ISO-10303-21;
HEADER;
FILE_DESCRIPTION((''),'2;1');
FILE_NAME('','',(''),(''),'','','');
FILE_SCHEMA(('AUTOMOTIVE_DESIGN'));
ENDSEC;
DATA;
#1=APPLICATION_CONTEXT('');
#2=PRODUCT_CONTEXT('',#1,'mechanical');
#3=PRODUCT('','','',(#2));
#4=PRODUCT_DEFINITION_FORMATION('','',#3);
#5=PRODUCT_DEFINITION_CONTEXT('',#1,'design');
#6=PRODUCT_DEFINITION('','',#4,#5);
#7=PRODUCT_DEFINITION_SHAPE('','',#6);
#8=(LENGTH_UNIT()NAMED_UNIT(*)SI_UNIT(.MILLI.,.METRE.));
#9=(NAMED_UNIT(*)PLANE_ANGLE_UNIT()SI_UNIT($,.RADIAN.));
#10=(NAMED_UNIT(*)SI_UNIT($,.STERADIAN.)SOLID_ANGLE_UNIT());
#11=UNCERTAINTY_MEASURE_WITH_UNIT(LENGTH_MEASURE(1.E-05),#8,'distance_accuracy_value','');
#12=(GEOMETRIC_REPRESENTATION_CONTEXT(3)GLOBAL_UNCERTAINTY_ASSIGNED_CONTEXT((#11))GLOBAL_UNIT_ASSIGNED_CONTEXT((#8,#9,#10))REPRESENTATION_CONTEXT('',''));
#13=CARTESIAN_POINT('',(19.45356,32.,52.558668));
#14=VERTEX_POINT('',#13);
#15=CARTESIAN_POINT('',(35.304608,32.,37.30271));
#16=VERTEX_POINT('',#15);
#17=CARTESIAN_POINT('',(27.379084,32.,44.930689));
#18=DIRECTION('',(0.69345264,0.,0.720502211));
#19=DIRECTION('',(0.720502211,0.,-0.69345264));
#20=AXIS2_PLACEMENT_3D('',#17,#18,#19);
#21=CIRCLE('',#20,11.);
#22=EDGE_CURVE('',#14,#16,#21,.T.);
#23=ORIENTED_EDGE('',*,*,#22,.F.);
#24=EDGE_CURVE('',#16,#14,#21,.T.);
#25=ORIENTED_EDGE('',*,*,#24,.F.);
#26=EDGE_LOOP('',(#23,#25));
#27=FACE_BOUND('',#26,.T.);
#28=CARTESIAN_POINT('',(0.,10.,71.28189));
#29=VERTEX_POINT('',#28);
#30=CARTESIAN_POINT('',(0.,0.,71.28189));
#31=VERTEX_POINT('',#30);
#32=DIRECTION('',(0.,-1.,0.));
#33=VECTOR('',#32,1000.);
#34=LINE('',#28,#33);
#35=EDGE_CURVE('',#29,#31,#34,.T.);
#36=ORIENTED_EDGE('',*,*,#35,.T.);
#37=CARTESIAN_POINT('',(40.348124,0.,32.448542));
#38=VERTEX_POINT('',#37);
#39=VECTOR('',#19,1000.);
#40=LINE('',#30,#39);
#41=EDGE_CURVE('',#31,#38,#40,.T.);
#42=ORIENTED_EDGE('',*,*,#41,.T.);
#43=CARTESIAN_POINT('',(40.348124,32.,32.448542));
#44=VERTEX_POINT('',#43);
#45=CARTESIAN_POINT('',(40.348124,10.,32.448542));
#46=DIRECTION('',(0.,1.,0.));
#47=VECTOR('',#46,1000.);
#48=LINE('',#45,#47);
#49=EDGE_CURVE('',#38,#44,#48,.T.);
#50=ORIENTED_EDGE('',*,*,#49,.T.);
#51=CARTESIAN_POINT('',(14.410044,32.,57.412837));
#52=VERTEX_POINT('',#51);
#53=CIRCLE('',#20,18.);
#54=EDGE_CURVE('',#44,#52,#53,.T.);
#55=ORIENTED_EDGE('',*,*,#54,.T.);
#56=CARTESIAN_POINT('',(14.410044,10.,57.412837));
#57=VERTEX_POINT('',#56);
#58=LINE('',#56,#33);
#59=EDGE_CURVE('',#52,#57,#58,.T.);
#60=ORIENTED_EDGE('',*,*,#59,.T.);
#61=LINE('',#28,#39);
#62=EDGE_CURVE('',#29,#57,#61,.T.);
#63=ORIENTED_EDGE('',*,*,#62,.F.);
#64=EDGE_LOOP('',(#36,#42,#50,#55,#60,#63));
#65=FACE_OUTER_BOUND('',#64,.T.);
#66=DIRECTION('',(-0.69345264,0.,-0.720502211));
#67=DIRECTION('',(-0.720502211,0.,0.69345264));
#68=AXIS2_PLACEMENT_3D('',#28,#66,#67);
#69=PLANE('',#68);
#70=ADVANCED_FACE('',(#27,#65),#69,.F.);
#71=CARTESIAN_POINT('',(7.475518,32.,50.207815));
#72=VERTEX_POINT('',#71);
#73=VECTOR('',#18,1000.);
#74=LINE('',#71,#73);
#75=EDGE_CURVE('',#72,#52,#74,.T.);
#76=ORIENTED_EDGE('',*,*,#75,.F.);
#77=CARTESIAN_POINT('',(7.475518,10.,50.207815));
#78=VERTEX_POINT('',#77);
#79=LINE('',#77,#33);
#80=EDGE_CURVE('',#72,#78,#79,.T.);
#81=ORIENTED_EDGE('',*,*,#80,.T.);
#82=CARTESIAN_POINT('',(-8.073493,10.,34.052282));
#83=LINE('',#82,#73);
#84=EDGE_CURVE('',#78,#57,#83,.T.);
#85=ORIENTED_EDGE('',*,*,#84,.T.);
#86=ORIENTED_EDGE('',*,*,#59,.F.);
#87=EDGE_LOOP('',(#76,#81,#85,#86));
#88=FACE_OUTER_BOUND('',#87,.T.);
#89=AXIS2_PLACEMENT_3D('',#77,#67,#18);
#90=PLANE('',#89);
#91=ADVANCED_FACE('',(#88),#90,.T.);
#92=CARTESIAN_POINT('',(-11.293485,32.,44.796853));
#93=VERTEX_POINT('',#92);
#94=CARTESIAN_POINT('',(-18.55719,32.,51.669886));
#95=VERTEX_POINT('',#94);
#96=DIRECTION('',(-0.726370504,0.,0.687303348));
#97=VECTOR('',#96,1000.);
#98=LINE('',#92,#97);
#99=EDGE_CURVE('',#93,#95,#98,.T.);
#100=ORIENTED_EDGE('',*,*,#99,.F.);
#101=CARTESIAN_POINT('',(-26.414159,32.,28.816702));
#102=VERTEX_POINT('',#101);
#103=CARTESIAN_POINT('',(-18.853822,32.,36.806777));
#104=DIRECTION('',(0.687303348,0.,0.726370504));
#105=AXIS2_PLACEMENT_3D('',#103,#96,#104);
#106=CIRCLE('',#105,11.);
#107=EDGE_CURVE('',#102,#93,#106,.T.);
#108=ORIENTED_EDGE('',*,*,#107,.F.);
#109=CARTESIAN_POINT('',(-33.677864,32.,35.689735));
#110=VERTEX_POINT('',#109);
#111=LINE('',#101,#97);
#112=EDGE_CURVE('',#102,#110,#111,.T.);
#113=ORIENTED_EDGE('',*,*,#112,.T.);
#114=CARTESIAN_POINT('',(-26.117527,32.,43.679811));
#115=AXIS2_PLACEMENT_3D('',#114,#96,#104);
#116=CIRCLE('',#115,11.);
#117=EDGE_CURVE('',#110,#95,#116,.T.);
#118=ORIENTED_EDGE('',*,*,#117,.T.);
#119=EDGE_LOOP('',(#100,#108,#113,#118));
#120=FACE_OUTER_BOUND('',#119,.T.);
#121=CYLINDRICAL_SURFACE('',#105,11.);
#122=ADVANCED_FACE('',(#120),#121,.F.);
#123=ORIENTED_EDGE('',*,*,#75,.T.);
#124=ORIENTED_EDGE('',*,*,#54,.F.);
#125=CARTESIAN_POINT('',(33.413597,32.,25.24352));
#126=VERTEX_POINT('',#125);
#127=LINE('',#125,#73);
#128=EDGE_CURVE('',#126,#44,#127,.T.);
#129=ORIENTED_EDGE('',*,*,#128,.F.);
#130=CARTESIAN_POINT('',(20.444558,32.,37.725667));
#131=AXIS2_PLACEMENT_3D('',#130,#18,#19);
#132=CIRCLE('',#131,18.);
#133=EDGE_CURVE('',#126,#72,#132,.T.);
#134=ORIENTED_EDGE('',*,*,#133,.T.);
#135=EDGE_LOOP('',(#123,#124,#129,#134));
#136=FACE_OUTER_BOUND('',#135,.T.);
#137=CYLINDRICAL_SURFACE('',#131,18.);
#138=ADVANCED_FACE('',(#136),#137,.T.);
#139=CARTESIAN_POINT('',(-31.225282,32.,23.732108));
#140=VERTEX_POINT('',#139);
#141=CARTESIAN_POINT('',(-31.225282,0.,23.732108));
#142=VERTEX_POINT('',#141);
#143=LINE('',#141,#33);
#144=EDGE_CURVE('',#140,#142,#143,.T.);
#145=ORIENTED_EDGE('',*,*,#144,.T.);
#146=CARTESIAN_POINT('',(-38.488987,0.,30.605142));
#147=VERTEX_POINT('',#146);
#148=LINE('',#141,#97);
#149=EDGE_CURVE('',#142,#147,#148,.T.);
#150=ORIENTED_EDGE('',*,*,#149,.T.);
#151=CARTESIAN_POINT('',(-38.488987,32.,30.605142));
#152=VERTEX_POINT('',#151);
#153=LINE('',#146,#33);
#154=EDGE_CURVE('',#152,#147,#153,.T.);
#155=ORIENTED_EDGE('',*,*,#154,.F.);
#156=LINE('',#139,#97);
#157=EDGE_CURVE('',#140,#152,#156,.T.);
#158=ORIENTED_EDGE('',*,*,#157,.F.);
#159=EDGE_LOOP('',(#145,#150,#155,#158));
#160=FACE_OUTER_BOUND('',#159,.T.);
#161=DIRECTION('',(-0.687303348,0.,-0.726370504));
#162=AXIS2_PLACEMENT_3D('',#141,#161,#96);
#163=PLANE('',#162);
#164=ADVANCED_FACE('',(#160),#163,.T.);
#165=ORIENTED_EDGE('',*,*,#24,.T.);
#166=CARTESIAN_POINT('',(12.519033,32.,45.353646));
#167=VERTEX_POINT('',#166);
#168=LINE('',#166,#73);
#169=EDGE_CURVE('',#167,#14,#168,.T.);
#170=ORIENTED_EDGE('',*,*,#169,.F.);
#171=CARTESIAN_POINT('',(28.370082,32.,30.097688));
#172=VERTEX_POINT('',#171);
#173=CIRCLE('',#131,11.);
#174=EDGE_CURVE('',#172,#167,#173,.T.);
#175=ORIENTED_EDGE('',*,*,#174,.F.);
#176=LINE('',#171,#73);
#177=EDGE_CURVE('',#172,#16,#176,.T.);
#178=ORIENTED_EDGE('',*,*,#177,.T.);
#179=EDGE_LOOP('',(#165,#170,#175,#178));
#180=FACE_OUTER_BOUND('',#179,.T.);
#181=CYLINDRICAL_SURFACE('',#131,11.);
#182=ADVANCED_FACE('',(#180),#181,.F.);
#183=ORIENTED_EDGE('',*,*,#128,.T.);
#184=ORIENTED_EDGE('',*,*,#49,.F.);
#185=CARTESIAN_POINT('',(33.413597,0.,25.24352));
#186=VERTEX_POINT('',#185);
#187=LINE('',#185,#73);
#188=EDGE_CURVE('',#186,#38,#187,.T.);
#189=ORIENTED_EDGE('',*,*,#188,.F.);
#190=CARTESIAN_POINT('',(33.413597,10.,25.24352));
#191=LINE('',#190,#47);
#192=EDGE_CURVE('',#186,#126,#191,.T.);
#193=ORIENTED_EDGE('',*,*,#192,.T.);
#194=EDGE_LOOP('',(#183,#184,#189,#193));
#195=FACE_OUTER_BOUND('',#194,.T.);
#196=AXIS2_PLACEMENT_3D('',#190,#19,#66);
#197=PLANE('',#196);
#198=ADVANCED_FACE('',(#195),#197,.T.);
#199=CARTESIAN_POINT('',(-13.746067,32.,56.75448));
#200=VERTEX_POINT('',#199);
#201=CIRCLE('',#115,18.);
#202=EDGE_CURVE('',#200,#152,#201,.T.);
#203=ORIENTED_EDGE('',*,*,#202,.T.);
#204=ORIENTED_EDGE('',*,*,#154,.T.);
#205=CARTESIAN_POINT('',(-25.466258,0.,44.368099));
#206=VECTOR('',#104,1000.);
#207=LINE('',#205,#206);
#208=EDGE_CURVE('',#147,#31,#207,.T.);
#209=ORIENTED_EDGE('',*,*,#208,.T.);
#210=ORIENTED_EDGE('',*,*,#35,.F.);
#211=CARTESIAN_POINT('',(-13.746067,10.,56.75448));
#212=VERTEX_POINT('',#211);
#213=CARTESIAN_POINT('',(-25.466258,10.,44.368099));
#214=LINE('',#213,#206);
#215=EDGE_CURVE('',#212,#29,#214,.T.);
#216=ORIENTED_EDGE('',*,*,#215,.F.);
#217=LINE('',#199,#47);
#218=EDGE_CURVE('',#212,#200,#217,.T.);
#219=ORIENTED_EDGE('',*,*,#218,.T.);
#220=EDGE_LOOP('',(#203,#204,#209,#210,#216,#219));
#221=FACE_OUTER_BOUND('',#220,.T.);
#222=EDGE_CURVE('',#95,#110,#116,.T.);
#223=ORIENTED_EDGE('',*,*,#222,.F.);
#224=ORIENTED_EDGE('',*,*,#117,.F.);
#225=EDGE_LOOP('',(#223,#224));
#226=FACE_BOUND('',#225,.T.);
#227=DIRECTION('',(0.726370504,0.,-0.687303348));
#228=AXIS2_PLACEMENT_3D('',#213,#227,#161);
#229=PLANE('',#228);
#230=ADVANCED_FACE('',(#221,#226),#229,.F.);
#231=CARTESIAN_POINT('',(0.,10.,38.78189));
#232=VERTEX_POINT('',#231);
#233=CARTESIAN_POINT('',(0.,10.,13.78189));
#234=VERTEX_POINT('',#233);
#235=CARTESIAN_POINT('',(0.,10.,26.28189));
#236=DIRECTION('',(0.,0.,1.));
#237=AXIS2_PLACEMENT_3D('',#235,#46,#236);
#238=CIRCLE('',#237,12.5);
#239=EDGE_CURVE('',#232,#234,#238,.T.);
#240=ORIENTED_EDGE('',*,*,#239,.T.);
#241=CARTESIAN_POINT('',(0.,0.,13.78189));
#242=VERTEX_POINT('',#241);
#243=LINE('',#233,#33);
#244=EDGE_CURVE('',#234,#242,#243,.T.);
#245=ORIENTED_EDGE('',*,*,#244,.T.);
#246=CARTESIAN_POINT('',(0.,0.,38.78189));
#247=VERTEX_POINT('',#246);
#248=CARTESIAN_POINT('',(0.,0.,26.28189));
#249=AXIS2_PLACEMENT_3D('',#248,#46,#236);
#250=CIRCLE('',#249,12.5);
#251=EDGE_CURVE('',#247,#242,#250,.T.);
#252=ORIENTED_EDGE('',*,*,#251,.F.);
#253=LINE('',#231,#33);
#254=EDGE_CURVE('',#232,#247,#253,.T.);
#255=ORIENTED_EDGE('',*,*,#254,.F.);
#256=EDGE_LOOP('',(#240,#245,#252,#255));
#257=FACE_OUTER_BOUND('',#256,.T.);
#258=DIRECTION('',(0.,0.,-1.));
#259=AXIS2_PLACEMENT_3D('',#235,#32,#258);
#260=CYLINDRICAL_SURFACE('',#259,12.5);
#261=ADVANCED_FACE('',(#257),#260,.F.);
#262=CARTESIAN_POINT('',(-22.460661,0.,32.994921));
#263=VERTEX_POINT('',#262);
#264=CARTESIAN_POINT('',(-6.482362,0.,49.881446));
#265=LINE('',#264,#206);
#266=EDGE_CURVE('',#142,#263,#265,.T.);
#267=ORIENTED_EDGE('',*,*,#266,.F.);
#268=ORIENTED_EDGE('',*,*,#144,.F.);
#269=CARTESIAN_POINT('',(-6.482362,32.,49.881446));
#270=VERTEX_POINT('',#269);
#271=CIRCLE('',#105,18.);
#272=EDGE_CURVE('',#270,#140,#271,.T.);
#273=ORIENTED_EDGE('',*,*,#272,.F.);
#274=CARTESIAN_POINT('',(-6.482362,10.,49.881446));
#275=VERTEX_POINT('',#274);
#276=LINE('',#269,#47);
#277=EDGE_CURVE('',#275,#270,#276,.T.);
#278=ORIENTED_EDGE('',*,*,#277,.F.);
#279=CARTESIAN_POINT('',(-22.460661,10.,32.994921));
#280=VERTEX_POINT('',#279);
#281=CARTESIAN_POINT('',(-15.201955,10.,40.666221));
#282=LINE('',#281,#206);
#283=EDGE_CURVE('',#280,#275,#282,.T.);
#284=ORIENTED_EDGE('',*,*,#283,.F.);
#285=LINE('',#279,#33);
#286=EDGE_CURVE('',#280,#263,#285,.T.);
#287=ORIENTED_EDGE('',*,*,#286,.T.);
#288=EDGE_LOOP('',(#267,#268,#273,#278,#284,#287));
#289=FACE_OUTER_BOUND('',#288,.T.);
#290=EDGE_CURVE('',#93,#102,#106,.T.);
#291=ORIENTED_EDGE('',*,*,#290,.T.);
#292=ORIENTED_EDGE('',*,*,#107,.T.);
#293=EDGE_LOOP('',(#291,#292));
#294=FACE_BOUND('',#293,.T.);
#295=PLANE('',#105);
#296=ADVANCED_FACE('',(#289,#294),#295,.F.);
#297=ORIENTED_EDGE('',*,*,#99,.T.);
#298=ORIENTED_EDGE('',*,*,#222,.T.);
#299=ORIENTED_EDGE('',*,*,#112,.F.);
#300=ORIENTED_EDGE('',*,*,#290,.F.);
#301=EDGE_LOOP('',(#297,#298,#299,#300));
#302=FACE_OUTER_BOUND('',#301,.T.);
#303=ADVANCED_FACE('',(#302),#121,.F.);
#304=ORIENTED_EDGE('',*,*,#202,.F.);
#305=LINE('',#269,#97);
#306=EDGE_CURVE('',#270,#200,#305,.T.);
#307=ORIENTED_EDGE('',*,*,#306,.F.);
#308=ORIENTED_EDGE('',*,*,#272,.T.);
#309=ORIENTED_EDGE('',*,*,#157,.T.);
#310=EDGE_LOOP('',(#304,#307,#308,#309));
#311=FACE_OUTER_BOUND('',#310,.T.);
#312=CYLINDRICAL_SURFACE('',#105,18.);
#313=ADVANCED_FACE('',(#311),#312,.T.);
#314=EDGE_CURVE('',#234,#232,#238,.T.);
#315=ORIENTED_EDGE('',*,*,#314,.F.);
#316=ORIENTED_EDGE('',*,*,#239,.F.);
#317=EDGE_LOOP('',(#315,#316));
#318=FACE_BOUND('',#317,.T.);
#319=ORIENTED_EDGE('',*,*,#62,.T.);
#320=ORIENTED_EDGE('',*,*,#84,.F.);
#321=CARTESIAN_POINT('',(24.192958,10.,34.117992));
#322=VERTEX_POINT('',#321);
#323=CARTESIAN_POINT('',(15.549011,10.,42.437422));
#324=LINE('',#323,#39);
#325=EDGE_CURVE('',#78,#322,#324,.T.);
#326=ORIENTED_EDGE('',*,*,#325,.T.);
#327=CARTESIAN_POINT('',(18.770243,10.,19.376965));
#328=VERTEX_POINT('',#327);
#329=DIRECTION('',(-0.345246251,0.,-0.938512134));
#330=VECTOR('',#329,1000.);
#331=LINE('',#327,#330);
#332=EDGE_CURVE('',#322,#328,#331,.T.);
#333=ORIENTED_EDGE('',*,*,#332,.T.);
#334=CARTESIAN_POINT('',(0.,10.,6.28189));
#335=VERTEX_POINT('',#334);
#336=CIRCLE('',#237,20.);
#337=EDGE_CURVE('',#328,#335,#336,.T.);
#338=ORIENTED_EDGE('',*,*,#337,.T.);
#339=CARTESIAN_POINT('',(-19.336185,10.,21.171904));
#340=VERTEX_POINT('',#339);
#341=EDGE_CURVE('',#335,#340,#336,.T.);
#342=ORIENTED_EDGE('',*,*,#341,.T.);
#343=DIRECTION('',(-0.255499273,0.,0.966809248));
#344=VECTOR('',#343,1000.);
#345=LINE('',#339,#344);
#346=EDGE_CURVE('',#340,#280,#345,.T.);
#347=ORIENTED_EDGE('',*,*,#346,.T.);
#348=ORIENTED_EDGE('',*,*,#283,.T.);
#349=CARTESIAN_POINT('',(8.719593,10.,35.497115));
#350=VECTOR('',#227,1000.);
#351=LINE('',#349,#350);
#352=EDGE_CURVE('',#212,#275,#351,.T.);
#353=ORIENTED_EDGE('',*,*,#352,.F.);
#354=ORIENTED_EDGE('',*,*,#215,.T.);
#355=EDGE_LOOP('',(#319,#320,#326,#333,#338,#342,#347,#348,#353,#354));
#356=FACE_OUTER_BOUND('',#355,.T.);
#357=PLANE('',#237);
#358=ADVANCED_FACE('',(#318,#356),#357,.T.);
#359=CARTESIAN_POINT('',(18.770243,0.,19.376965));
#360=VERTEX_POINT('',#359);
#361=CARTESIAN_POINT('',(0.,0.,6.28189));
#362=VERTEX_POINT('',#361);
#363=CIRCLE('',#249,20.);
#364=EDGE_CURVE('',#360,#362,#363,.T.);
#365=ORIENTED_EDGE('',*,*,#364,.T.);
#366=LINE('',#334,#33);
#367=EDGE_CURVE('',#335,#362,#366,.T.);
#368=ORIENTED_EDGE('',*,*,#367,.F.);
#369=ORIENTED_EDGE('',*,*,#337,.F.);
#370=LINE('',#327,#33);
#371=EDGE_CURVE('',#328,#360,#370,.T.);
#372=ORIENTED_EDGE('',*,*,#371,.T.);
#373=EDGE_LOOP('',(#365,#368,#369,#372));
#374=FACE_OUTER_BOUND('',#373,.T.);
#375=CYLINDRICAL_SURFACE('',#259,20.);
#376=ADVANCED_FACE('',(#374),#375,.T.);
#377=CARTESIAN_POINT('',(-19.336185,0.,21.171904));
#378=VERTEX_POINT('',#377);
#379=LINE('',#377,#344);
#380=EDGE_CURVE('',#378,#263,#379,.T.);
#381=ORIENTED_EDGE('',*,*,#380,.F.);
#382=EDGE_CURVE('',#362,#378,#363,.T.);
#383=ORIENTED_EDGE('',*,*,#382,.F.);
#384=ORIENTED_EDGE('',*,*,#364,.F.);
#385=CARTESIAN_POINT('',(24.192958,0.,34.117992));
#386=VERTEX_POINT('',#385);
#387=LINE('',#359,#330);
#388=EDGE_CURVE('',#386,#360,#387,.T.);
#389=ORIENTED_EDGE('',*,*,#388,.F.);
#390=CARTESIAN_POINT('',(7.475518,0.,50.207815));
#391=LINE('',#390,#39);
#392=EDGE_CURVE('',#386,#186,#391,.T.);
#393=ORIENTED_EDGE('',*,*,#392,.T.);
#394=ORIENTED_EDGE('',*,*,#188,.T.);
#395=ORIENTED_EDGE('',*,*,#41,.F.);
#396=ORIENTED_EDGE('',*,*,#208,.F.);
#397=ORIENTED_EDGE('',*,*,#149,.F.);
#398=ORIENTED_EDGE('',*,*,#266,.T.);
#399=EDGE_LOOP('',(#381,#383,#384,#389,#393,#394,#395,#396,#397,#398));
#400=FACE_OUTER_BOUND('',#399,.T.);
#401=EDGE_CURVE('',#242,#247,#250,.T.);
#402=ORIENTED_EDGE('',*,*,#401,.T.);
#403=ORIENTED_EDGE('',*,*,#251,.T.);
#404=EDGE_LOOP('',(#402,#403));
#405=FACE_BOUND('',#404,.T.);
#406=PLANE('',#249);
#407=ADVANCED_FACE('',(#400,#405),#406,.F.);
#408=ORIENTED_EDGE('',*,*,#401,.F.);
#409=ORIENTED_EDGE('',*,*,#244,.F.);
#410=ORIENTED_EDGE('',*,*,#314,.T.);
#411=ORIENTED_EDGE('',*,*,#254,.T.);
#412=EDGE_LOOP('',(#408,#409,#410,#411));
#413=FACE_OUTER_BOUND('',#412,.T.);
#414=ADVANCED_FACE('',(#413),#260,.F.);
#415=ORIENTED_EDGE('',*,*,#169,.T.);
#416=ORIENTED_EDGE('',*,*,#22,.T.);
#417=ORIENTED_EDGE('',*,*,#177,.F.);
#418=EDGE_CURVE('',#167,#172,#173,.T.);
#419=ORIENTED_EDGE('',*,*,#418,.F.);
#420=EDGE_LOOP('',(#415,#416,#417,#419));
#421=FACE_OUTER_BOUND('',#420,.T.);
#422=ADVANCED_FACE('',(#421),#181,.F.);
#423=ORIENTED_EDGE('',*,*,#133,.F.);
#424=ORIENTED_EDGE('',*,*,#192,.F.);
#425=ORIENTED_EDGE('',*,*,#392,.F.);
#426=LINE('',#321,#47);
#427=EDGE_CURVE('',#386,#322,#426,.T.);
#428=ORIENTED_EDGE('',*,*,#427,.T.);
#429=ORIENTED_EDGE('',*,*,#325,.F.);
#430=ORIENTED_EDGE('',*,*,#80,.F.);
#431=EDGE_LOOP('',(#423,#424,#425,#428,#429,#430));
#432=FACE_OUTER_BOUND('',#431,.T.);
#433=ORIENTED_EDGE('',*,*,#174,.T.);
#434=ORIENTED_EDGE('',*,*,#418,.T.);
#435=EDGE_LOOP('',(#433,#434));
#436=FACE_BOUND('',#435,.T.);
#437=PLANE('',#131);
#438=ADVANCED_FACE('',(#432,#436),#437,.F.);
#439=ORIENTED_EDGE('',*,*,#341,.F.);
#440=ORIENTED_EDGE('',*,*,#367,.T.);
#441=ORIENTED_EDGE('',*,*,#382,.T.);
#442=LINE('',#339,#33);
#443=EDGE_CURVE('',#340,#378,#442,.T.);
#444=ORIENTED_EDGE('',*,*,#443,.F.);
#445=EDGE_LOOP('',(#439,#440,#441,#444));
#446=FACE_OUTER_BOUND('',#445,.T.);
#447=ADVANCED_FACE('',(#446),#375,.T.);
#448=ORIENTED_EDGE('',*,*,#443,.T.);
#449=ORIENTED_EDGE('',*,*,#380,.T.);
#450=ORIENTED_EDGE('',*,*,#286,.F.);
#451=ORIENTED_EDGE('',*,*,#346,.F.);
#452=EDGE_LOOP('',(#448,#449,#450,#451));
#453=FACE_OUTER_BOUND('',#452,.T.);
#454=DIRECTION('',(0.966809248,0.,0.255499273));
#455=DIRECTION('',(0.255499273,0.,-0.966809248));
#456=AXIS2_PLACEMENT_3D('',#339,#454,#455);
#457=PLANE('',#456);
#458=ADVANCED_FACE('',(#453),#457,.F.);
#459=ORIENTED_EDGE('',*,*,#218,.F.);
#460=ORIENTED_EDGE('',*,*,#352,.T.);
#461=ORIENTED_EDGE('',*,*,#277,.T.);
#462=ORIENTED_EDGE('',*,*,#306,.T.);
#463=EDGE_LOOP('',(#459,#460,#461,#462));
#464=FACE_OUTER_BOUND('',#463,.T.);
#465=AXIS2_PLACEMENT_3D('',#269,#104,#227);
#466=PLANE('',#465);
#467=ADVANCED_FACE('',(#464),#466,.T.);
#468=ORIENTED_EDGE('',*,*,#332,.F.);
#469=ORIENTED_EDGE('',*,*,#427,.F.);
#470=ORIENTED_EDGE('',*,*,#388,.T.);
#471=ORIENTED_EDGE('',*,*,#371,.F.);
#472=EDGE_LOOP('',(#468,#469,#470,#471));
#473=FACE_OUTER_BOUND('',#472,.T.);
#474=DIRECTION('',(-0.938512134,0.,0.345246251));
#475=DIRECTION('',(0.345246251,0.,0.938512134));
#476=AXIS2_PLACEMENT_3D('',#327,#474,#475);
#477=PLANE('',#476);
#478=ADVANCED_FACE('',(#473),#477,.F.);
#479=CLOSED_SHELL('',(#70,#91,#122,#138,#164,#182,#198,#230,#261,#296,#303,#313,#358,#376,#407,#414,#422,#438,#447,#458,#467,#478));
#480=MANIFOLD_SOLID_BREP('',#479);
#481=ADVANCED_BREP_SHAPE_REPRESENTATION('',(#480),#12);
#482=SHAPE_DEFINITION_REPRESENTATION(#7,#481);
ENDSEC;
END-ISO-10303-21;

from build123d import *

# Parameters (mm, degrees)
BASE_PLATE_SKETCH_R = 12.5
BASE_PLATE_DEPTH    = 10
LUG_1_SKETCH_R      = 11
LUG_1_DEPTH         = 10
LUG_2_SKETCH_R      = 11
LUG_2_DEPTH         = 10


with BuildPart() as part:
    # Base Plate Sketch → Base Plate (new body)
    with BuildSketch(Plane(origin=(0, 0, 0), x_dir=(1, 0, 0), z_dir=(0, 1, 0))):
        with BuildLine():
            Line((-19.336184956, -21.171904289), (-25.4662576, -44.368099172))
            Line((-25.4662576, -44.368099172), (0, -71.281889743))
            Line((0, -71.281889743), (27.963619281, -44.368099172))
            Line((27.963619281, -44.368099172), (18.770242682, -19.376964714))
            ThreePointArc((18.770242682, -19.376964714), (-0.941023212, -6.304040126), (-19.336184956, -21.171904289))
        make_face()
        with Locations(Location((0, -26.281889743, 0), (0, 0, 270))):
            Circle(BASE_PLATE_SKETCH_R, mode=Mode.SUBTRACT)
    extrude(amount=BASE_PLATE_DEPTH)

    # Lug 1 Sketch → Lug 1 (add)
    with BuildSketch(Plane(origin=(35.61486713, 0, 37.004099536), x_dir=(0.720502211038311, 0, -0.6934526399754386), z_dir=(0.6934526399754386, 0, 0.720502211038311))):
        with BuildLine():
            Line((-29.430614625, 10), (-29.430614625, 32))
            ThreePointArc((-29.430614625, 32), (-11.430614625, 50), (6.569385375, 32))
            Line((6.569385375, 32), (6.569385375, 10))
            Line((6.569385375, 10), (6.569385375, 0))
            Line((6.569385375, 0), (-29.430614625, 0))
            Line((-29.430614625, 0), (-29.430614625, 10))
        make_face()
        with Locations((-11.430614625, 32)):
            Circle(LUG_1_SKETCH_R, mode=Mode.SUBTRACT)
    extrude(amount=-LUG_1_DEPTH)

    # Lug 2 Sketch → Lug 2 (add)
    with BuildSketch(Plane(origin=(-35.586548141, 0, 33.672559042), x_dir=(0.6873033475884168, 0, 0.7263705035267854), z_dir=(-0.7263705035267854, 0, 0.6873033475884168))):
        with BuildLine():
            Line((31.777062145, 32), (31.777062145, 0))
            Line((31.777062145, 0), (-4.222937855, 0))
            Line((-4.222937855, 0), (-4.222937855, 32))
            ThreePointArc((-4.222937855, 32), (13.777062145, 50), (31.777062145, 32))
        make_face()
        with Locations((13.777062145, 32)):
            Circle(LUG_2_SKETCH_R, mode=Mode.SUBTRACT)
    extrude(amount=-LUG_2_DEPTH)


solid = part.part
